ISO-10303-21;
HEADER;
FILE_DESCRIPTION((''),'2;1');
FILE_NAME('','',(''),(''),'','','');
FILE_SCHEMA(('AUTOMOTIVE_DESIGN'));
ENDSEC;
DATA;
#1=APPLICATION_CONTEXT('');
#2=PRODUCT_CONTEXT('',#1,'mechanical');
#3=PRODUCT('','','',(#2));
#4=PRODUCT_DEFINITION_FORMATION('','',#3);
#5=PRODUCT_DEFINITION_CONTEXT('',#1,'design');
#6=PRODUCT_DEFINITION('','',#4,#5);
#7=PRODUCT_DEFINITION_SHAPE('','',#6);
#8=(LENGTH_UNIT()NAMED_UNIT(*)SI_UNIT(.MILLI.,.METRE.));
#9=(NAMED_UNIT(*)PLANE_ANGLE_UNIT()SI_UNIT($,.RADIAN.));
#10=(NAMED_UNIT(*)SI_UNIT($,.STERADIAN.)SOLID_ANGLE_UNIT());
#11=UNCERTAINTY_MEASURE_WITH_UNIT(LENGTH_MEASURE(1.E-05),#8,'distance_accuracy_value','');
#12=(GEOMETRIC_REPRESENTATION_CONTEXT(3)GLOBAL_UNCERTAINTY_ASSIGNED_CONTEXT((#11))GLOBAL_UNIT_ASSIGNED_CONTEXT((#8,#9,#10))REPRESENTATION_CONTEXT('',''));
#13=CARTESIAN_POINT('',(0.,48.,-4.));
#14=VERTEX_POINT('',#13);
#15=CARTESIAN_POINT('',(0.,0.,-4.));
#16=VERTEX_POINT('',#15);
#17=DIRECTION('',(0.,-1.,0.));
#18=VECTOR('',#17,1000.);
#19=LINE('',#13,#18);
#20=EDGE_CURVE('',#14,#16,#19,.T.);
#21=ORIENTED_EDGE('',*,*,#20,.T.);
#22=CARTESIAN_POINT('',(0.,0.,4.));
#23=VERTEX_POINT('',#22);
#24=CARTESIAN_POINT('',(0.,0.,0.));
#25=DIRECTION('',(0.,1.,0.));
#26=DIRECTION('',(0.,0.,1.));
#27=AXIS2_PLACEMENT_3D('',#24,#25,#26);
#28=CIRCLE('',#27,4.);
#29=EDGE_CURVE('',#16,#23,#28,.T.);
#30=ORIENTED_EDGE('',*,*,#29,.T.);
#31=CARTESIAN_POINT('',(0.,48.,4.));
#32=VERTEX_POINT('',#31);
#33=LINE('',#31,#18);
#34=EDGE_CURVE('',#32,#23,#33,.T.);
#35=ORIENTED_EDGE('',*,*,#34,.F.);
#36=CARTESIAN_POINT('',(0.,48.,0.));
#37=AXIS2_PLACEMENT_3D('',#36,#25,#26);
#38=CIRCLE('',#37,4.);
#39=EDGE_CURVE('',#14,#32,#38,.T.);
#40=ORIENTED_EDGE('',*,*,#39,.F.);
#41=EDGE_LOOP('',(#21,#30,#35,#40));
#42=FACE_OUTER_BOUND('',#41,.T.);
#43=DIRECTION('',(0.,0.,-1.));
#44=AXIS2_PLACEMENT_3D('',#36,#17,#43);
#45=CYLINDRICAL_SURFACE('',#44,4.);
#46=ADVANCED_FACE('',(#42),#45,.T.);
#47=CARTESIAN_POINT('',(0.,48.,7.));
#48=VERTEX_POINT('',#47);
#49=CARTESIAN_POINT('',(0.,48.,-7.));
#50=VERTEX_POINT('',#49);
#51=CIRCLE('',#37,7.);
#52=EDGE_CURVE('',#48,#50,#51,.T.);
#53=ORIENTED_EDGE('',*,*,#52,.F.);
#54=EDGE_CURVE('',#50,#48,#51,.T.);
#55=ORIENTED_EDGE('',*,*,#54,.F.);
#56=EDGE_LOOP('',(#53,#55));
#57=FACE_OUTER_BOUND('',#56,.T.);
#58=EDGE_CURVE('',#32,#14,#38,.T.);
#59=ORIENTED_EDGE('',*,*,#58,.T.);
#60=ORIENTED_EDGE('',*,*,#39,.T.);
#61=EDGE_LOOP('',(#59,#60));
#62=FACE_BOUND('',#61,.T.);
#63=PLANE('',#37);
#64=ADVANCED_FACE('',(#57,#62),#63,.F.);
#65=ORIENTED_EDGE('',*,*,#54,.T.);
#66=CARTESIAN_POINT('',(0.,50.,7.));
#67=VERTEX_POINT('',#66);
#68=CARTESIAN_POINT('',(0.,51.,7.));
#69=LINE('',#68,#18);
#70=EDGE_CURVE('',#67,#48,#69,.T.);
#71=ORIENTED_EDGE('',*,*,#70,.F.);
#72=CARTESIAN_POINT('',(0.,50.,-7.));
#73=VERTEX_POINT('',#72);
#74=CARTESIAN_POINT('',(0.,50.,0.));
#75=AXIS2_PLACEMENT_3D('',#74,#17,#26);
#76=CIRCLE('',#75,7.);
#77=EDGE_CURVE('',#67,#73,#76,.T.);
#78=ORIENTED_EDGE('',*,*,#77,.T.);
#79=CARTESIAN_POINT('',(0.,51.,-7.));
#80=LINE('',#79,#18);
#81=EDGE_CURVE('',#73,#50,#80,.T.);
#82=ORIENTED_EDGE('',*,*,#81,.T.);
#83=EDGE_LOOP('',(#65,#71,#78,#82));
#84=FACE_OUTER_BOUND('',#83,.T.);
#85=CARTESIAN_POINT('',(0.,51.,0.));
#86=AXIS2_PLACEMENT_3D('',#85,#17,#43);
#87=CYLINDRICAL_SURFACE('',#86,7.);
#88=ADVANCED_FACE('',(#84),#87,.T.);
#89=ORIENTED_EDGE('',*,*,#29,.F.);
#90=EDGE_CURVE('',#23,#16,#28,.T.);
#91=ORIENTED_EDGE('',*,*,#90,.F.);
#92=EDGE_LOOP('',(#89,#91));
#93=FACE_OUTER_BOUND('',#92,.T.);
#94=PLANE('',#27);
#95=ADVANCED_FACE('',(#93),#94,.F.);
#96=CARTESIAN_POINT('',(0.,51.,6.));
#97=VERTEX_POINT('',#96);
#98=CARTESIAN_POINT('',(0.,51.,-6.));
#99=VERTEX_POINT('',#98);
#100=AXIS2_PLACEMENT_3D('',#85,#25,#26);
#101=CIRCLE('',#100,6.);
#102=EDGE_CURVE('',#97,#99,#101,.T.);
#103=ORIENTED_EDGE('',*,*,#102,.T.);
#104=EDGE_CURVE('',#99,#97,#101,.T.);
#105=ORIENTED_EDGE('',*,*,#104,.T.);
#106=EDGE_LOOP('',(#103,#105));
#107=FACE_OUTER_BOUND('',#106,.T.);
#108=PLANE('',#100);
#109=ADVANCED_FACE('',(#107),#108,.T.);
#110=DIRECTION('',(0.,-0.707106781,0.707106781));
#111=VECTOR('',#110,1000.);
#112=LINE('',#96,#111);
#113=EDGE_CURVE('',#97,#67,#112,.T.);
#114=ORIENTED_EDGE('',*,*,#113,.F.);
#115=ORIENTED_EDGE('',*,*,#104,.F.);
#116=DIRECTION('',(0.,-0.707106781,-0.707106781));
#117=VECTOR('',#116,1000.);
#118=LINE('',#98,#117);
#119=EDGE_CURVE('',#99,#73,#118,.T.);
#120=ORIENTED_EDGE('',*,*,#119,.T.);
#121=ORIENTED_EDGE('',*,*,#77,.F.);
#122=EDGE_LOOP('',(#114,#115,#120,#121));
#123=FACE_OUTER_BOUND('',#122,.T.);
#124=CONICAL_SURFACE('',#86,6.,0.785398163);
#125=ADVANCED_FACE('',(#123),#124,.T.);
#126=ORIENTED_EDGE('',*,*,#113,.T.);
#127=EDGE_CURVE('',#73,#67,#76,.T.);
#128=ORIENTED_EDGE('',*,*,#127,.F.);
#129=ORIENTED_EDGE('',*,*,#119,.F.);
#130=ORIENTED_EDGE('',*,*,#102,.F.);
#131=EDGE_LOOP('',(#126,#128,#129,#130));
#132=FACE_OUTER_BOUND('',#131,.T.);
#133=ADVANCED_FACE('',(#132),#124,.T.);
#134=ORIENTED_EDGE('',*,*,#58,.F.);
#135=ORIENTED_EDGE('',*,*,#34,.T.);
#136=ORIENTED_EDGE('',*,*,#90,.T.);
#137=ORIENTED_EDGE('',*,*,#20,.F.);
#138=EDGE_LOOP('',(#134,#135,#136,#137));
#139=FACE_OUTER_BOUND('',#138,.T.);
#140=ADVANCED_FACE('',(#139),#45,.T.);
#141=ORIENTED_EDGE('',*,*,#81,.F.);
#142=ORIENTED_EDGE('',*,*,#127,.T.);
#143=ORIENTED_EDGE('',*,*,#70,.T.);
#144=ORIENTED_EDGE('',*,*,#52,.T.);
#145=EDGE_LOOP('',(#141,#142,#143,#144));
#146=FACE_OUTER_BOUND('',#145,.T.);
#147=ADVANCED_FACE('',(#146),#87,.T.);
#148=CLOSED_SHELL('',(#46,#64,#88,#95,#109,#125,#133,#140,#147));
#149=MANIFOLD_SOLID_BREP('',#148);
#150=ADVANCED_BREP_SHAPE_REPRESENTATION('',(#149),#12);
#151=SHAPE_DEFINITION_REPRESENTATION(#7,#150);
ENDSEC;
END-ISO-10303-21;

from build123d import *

# Parameters (mm, degrees)
SHANK_PROFILE_8_R      = 4
SHANK_8X48_DEPTH       = 48
HEAD_PROFILE_14_R      = 7
HEAD_14X3_DEPTH        = 3
HEAD_CHAMFER_1X45_SIZE = 1


with BuildPart() as part:
    # Shank Profile Ø8 → Shank Ø8x48 (new body)
    with BuildSketch(Plane(origin=(0, 0, 0), x_dir=(1, 0, 0), z_dir=(0, 1, 0))):
        with Locations(Location((0, 0, 0), (0, 0, 270))):
            Circle(SHANK_PROFILE_8_R)
    extrude(amount=SHANK_8X48_DEPTH)

    # Head Profile Ø14 → Head Ø14x3 (add)
    with BuildSketch(Plane(origin=(0, 48, 0), x_dir=(1, 0, 0), z_dir=(0, 1, 0))):
        with Locations(Location((0, 0, 0), (0, 0, 270))):
            Circle(HEAD_PROFILE_14_R)
    extrude(amount=HEAD_14X3_DEPTH)

    # Head Chamfer 1x45°
    head_chamfer_1x45_edges = [part.edges().sort_by_distance(p)[0] for p in [
        (0, 51, -7),
    ]]
    chamfer(head_chamfer_1x45_edges, length=HEAD_CHAMFER_1X45_SIZE)


solid = part.part
